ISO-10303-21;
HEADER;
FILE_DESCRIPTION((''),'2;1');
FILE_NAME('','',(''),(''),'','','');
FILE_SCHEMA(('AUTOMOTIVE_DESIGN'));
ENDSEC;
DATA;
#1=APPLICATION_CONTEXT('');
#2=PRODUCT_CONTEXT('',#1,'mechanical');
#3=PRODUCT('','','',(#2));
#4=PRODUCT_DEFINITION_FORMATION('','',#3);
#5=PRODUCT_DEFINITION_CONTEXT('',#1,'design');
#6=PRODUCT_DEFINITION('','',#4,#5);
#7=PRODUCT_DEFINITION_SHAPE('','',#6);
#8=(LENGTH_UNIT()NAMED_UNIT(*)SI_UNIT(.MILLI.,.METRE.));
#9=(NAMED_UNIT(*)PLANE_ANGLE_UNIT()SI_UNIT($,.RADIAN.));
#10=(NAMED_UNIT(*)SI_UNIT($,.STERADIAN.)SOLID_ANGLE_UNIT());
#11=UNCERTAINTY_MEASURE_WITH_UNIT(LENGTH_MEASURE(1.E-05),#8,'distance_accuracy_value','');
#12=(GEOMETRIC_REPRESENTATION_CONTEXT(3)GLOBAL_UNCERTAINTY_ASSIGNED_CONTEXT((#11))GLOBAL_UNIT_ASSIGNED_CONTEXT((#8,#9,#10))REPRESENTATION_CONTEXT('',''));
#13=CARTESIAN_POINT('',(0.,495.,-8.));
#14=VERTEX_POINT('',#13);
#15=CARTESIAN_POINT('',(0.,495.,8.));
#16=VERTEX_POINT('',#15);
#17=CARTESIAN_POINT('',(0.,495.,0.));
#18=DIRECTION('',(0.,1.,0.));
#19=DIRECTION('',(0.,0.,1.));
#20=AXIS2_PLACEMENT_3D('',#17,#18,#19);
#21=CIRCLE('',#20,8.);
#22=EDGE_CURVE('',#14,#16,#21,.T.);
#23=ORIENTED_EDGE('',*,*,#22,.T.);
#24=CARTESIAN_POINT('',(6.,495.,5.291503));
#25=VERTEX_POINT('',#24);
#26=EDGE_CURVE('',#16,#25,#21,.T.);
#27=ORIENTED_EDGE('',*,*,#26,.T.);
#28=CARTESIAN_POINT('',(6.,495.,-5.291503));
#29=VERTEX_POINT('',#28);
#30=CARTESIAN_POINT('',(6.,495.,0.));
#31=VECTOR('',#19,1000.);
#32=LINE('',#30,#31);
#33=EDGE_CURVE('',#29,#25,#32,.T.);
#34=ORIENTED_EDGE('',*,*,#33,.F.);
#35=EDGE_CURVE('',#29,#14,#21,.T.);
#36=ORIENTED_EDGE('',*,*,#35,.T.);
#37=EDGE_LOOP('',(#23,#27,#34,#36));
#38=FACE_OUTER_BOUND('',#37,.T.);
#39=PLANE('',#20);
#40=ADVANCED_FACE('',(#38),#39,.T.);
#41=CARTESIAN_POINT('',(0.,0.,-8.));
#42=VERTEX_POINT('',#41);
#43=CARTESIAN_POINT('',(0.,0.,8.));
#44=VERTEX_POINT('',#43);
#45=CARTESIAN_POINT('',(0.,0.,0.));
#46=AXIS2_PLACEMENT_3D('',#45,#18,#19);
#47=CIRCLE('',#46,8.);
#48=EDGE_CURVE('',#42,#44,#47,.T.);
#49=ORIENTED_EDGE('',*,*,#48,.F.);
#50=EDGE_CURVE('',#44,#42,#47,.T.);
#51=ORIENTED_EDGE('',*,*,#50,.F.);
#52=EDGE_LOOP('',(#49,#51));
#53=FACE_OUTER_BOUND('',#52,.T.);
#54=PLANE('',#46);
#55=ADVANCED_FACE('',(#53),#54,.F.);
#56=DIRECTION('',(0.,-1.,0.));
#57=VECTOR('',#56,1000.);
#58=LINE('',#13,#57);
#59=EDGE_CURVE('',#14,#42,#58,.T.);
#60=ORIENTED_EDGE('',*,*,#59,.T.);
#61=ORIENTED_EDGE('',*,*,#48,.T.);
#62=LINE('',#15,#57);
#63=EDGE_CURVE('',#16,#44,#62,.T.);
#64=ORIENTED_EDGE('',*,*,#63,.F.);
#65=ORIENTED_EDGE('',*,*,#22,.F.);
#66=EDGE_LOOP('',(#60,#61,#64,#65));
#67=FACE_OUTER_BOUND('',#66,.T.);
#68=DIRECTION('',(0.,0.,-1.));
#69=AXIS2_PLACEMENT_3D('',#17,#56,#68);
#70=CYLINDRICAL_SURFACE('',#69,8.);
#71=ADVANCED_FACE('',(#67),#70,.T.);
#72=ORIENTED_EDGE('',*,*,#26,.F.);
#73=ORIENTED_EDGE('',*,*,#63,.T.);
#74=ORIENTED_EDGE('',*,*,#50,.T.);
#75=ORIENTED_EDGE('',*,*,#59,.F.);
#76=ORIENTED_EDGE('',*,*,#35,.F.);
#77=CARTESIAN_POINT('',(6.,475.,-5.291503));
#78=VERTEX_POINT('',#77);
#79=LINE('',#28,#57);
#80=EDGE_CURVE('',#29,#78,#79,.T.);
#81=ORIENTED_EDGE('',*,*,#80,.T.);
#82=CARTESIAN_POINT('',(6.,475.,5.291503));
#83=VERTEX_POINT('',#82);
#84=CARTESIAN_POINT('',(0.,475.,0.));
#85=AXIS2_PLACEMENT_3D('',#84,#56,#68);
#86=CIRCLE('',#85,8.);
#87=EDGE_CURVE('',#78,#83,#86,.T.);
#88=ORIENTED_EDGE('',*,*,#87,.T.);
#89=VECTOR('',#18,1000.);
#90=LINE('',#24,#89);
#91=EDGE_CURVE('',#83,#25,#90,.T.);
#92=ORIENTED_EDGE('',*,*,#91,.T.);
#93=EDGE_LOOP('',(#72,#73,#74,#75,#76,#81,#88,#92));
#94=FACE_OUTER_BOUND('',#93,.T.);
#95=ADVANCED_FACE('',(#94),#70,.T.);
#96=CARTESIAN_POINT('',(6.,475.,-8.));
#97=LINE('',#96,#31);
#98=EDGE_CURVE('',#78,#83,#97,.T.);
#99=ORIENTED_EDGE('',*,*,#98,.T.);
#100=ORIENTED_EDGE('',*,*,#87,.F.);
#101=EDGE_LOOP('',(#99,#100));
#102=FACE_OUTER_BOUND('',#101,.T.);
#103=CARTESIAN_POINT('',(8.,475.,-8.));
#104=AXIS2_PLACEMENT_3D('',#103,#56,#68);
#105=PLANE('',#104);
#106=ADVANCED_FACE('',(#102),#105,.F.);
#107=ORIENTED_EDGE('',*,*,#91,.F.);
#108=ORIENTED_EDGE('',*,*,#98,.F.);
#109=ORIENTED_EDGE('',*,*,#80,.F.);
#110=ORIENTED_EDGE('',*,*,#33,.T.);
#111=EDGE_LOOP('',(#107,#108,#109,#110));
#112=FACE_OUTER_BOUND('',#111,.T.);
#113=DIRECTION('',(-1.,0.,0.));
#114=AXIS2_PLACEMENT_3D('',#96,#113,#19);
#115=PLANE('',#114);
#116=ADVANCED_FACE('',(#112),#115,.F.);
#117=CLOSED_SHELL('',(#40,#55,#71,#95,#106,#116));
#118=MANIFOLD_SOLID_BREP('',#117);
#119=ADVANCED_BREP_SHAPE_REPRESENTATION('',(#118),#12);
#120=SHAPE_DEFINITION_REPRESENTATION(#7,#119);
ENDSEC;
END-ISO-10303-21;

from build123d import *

# Parameters (mm, degrees)
SKETCH1_R               = 8
BOSS_EXTRUDE1_DEPTH     = 495
CUT_EXTRUDE1_DEPTH      = 496.129276048
CUT_EXTRUDE1_DEPTH_BACK = 496.129276048
SKETCH2_W               = 2
SKETCH2_H               = 20


with BuildPart() as part:
    # Sketch1 → Boss-Extrude1 (new body)
    with BuildSketch(Plane(origin=(0, 0, 0), x_dir=(1, 0, 0), z_dir=(0, 1, 0))):
        with Locations(Location((0, 0, 0), (0, 0, 270))):
            Circle(SKETCH1_R)
    extrude(amount=BOSS_EXTRUDE1_DEPTH)

    # Sketch2 → Cut-Extrude1 (cut, two sides: drawn at the far end of the back side and taken through both)
    with BuildSketch(Plane.XY.offset(-CUT_EXTRUDE1_DEPTH_BACK)):
        with Locations((7, 485)):
            Rectangle(SKETCH2_W, SKETCH2_H)
    extrude(amount=CUT_EXTRUDE1_DEPTH + CUT_EXTRUDE1_DEPTH_BACK, mode=Mode.SUBTRACT)


solid = part.part
